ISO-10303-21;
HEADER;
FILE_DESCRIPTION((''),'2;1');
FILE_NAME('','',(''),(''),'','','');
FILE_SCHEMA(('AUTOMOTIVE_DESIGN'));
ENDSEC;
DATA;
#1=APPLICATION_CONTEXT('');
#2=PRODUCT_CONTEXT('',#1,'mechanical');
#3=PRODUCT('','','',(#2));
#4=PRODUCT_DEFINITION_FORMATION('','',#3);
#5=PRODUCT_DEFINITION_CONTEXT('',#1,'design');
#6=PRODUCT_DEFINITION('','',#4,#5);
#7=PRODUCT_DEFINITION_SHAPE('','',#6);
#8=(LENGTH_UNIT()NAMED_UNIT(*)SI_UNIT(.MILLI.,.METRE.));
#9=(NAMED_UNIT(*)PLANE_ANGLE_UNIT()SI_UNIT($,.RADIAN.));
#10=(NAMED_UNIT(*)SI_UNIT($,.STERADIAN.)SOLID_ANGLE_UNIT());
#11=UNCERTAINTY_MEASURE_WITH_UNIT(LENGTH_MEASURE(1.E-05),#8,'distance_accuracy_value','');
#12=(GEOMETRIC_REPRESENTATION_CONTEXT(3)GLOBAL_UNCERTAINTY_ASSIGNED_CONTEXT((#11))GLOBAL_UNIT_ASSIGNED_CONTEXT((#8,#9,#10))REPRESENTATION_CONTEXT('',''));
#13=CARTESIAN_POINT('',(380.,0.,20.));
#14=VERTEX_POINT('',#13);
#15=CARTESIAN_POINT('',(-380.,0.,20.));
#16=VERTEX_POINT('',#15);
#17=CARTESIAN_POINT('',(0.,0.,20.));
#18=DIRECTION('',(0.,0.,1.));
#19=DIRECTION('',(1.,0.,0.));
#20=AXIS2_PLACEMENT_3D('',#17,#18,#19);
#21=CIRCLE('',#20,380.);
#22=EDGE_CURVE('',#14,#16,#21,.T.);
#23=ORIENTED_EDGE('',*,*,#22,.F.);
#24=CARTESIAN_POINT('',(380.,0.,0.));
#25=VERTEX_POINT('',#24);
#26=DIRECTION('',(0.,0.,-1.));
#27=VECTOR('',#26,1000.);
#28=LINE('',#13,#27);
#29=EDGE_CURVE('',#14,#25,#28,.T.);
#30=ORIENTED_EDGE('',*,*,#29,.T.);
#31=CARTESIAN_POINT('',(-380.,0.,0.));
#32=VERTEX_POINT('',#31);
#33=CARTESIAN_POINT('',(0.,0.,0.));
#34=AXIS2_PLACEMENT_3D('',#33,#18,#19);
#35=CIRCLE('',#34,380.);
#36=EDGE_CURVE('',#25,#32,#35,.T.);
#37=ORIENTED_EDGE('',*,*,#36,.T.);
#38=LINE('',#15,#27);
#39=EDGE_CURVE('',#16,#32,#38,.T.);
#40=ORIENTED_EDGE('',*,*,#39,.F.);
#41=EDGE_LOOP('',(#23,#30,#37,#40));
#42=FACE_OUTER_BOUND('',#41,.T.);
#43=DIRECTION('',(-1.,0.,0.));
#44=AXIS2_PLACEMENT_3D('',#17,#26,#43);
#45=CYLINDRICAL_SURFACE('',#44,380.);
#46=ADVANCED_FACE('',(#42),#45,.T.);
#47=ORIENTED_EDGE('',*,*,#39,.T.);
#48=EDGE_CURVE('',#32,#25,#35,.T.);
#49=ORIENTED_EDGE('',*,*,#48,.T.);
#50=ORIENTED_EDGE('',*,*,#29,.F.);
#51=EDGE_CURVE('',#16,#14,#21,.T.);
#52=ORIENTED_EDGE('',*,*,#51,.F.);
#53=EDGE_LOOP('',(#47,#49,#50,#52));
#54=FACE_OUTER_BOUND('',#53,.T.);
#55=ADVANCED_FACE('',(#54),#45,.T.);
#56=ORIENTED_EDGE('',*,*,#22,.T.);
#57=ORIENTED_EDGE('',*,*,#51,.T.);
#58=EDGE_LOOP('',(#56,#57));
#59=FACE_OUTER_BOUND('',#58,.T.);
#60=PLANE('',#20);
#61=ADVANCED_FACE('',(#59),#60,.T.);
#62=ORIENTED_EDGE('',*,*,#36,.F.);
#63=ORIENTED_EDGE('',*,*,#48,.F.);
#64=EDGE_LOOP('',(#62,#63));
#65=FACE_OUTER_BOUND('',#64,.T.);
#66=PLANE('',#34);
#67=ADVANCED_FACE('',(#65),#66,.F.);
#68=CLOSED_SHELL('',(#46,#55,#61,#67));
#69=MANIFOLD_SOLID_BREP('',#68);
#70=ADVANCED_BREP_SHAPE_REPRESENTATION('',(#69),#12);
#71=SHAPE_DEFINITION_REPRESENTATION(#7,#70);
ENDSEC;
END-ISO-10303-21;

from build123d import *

# Parameters (mm, degrees)
SKETCH1_R           = 380
BOSS_EXTRUDE1_DEPTH = 20


with BuildPart() as part:
    # Sketch1 → Boss-Extrude1 (new body)
    with BuildSketch(Plane.XY):
        Circle(SKETCH1_R)
    extrude(amount=BOSS_EXTRUDE1_DEPTH)


solid = part.part
